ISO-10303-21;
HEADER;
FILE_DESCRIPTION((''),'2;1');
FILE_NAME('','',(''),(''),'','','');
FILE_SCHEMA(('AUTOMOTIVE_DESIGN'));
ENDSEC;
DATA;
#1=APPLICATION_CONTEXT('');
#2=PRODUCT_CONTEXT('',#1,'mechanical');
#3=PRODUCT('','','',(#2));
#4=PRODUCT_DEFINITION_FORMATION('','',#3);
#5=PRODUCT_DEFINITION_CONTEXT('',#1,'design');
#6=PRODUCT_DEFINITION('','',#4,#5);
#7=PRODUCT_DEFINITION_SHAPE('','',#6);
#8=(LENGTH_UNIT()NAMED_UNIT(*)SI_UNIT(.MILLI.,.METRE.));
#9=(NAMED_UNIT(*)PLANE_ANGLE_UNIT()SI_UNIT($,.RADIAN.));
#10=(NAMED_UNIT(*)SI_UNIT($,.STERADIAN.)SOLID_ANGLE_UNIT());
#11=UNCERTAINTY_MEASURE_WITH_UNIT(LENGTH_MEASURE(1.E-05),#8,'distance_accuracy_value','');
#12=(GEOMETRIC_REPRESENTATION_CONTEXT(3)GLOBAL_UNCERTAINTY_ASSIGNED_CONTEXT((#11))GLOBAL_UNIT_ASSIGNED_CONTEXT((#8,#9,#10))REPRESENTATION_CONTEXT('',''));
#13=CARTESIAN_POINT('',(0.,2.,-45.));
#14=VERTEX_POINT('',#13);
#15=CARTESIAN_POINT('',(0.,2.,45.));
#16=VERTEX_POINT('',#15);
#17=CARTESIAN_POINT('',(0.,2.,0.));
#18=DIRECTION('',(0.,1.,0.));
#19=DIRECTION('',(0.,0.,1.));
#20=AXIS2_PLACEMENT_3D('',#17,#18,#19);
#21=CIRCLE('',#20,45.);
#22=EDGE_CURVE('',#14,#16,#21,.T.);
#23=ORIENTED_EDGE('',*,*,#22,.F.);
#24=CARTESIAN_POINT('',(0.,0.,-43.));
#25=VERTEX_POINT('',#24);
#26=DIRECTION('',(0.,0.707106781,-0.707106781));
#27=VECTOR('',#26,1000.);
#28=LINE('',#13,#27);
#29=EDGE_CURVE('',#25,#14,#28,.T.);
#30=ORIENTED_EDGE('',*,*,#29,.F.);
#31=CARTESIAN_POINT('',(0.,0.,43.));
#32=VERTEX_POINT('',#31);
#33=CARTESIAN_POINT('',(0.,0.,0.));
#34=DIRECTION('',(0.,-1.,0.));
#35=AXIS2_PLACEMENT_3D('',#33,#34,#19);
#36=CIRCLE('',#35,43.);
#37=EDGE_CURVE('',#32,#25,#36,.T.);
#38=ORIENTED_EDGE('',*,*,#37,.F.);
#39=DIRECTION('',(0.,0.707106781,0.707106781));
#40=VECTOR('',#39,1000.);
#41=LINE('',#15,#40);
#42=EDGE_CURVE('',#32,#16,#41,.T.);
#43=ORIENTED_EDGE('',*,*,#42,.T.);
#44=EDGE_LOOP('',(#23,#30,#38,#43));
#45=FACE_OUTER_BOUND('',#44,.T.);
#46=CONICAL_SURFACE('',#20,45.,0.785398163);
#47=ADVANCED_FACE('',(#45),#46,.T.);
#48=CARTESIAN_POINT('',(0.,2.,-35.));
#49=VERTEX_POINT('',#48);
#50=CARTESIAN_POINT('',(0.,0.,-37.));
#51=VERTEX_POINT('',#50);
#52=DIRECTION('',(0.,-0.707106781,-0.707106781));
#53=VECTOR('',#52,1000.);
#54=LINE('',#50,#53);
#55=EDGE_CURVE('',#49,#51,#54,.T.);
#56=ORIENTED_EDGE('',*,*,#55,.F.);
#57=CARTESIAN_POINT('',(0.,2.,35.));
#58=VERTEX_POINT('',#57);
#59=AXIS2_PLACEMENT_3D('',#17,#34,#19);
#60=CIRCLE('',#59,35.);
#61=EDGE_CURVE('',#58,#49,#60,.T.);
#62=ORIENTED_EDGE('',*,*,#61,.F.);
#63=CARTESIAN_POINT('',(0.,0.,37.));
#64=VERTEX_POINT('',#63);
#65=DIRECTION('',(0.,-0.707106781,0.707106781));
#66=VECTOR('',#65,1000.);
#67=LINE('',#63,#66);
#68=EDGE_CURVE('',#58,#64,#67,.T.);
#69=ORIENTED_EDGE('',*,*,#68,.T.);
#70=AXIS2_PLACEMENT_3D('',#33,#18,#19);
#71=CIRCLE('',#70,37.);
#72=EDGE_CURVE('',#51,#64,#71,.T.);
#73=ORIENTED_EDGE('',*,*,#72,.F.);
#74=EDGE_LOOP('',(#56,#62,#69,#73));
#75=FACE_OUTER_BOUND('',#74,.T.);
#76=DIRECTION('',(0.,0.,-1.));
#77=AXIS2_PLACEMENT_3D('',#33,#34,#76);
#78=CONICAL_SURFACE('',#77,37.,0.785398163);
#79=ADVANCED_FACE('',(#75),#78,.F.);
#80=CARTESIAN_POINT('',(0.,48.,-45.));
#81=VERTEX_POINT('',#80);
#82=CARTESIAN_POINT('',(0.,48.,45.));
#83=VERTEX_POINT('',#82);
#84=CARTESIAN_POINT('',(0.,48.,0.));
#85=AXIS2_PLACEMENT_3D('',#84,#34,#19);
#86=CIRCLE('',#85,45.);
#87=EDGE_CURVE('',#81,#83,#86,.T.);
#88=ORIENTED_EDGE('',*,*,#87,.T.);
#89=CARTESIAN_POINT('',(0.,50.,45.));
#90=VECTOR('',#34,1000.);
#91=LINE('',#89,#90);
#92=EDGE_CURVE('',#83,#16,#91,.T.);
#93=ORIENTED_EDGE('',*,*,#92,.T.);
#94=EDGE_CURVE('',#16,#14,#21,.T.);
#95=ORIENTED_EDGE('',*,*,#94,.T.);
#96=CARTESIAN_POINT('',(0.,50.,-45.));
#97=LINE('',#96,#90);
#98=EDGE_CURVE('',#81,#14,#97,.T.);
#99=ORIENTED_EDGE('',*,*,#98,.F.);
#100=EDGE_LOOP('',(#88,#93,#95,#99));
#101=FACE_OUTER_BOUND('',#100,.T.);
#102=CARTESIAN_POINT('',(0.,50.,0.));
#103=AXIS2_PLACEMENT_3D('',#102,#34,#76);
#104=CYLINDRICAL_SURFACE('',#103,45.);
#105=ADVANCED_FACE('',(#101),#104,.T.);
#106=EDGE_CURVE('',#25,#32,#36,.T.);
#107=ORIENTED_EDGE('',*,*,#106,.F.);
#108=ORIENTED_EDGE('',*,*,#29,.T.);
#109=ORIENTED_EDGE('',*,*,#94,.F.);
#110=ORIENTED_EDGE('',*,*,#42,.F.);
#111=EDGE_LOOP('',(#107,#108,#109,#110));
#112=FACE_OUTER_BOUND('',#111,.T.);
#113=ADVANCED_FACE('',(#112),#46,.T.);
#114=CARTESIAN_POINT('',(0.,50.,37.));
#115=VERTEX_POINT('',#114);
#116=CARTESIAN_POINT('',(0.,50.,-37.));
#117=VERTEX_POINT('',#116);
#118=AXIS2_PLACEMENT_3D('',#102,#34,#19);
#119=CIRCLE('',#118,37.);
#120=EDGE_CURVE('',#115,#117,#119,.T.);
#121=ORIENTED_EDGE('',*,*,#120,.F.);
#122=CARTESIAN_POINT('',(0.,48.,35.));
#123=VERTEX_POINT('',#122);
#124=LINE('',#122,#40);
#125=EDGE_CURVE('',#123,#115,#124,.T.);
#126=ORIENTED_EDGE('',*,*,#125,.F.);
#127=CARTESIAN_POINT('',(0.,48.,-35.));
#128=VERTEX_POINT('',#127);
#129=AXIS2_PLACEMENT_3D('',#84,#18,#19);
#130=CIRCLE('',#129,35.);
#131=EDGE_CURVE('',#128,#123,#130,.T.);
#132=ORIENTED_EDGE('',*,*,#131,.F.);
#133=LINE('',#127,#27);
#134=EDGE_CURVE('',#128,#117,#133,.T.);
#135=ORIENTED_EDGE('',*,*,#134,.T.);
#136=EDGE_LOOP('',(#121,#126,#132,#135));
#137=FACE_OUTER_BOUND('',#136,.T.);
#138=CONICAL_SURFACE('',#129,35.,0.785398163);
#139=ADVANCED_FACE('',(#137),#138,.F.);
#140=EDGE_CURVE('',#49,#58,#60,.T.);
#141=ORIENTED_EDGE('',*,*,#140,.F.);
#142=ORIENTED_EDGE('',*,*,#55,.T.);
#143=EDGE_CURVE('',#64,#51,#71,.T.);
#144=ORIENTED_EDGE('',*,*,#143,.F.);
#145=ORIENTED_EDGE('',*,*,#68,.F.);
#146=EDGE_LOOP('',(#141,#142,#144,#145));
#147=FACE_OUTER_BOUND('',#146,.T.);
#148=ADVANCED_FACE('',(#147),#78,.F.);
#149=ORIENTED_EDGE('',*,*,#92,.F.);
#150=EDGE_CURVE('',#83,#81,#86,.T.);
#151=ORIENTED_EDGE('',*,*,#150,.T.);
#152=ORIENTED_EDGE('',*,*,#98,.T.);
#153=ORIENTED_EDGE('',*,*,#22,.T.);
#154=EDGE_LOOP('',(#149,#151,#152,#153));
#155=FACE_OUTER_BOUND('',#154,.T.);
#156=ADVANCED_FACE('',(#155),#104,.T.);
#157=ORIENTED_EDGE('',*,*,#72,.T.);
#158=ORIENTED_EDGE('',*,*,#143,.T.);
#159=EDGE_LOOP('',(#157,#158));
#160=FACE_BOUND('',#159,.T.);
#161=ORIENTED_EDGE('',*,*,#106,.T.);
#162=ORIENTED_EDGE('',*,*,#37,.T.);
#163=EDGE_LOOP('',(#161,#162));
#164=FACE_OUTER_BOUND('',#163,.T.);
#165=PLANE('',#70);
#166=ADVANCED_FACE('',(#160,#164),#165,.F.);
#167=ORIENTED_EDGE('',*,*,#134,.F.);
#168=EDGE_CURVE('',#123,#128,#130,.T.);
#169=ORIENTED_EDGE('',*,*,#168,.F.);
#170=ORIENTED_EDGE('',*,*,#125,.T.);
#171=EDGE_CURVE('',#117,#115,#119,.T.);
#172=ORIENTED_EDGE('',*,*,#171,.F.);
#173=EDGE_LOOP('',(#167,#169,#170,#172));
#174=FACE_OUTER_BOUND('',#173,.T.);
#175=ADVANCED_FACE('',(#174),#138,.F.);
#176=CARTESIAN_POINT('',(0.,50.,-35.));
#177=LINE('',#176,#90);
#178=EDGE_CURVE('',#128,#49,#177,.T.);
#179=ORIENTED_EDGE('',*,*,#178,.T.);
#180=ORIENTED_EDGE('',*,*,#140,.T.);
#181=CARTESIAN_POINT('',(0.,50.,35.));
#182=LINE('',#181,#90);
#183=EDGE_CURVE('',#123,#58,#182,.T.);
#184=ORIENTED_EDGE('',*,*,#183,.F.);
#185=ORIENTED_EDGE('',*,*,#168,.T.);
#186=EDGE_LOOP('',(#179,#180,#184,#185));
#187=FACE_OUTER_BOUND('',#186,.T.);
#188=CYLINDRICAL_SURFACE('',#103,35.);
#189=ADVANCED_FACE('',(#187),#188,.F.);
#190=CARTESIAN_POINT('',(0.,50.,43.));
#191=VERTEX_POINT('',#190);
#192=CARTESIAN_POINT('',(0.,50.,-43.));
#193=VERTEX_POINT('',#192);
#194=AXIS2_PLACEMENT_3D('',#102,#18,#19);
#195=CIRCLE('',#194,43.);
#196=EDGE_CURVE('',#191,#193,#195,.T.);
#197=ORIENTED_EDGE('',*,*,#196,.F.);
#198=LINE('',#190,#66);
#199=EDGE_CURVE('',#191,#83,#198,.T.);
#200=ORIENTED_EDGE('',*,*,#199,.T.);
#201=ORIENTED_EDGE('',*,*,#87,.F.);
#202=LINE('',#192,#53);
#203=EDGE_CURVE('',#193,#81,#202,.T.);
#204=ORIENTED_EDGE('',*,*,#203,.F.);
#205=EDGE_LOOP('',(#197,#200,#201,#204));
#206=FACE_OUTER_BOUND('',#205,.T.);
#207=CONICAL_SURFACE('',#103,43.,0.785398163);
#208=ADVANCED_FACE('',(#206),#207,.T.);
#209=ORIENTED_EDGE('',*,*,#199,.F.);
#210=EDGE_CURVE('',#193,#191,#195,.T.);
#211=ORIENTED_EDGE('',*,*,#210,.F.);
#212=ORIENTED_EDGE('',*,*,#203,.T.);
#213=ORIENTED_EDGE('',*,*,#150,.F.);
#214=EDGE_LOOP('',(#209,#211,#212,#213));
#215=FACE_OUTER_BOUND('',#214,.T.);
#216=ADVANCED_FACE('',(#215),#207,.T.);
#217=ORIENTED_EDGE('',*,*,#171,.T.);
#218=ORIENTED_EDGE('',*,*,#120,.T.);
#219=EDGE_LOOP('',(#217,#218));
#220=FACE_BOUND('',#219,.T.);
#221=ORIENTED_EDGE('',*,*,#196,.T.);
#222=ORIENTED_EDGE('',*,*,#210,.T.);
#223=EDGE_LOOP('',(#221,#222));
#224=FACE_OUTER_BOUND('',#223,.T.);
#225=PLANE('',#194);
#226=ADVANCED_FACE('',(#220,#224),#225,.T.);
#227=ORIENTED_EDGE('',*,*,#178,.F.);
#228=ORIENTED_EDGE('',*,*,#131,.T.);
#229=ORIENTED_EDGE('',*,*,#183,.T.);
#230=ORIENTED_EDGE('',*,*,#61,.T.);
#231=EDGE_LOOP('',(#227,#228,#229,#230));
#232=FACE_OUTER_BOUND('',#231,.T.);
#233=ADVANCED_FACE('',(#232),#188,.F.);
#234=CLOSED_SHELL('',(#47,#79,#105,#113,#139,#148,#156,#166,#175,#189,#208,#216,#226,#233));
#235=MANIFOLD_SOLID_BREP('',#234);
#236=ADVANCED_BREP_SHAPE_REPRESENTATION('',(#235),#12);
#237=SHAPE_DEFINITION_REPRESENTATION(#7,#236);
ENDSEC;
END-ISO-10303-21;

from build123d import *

# Parameters (mm, degrees)
SKETCH1_R           = 45
SKETCH1_R_2         = 35
BOSS_EXTRUDE1_DEPTH = 50
CHAMFER2_SIZE       = 2


with BuildPart() as part:
    # Sketch1 → Boss-Extrude1 (new body)
    with BuildSketch(Plane(origin=(0, 0, 0), x_dir=(1, 0, 0), z_dir=(0, 1, 0))):
        with Locations(Location((0, 0, 0), (0, 0, 270))):
            Circle(SKETCH1_R)
        with Locations(Location((0, 0, 0), (0, 0, 270))):
            Circle(SKETCH1_R_2, mode=Mode.SUBTRACT)
    extrude(amount=BOSS_EXTRUDE1_DEPTH)

    # Chamfer2
    chamfer2_edges = [part.edges().sort_by_distance(p)[0] for p in [
        (0, 0, -45),
        (0, 50, -45),
        (0, 0, -35),
        (0, 50, -35),
    ]]
    chamfer(chamfer2_edges, length=CHAMFER2_SIZE)


solid = part.part
